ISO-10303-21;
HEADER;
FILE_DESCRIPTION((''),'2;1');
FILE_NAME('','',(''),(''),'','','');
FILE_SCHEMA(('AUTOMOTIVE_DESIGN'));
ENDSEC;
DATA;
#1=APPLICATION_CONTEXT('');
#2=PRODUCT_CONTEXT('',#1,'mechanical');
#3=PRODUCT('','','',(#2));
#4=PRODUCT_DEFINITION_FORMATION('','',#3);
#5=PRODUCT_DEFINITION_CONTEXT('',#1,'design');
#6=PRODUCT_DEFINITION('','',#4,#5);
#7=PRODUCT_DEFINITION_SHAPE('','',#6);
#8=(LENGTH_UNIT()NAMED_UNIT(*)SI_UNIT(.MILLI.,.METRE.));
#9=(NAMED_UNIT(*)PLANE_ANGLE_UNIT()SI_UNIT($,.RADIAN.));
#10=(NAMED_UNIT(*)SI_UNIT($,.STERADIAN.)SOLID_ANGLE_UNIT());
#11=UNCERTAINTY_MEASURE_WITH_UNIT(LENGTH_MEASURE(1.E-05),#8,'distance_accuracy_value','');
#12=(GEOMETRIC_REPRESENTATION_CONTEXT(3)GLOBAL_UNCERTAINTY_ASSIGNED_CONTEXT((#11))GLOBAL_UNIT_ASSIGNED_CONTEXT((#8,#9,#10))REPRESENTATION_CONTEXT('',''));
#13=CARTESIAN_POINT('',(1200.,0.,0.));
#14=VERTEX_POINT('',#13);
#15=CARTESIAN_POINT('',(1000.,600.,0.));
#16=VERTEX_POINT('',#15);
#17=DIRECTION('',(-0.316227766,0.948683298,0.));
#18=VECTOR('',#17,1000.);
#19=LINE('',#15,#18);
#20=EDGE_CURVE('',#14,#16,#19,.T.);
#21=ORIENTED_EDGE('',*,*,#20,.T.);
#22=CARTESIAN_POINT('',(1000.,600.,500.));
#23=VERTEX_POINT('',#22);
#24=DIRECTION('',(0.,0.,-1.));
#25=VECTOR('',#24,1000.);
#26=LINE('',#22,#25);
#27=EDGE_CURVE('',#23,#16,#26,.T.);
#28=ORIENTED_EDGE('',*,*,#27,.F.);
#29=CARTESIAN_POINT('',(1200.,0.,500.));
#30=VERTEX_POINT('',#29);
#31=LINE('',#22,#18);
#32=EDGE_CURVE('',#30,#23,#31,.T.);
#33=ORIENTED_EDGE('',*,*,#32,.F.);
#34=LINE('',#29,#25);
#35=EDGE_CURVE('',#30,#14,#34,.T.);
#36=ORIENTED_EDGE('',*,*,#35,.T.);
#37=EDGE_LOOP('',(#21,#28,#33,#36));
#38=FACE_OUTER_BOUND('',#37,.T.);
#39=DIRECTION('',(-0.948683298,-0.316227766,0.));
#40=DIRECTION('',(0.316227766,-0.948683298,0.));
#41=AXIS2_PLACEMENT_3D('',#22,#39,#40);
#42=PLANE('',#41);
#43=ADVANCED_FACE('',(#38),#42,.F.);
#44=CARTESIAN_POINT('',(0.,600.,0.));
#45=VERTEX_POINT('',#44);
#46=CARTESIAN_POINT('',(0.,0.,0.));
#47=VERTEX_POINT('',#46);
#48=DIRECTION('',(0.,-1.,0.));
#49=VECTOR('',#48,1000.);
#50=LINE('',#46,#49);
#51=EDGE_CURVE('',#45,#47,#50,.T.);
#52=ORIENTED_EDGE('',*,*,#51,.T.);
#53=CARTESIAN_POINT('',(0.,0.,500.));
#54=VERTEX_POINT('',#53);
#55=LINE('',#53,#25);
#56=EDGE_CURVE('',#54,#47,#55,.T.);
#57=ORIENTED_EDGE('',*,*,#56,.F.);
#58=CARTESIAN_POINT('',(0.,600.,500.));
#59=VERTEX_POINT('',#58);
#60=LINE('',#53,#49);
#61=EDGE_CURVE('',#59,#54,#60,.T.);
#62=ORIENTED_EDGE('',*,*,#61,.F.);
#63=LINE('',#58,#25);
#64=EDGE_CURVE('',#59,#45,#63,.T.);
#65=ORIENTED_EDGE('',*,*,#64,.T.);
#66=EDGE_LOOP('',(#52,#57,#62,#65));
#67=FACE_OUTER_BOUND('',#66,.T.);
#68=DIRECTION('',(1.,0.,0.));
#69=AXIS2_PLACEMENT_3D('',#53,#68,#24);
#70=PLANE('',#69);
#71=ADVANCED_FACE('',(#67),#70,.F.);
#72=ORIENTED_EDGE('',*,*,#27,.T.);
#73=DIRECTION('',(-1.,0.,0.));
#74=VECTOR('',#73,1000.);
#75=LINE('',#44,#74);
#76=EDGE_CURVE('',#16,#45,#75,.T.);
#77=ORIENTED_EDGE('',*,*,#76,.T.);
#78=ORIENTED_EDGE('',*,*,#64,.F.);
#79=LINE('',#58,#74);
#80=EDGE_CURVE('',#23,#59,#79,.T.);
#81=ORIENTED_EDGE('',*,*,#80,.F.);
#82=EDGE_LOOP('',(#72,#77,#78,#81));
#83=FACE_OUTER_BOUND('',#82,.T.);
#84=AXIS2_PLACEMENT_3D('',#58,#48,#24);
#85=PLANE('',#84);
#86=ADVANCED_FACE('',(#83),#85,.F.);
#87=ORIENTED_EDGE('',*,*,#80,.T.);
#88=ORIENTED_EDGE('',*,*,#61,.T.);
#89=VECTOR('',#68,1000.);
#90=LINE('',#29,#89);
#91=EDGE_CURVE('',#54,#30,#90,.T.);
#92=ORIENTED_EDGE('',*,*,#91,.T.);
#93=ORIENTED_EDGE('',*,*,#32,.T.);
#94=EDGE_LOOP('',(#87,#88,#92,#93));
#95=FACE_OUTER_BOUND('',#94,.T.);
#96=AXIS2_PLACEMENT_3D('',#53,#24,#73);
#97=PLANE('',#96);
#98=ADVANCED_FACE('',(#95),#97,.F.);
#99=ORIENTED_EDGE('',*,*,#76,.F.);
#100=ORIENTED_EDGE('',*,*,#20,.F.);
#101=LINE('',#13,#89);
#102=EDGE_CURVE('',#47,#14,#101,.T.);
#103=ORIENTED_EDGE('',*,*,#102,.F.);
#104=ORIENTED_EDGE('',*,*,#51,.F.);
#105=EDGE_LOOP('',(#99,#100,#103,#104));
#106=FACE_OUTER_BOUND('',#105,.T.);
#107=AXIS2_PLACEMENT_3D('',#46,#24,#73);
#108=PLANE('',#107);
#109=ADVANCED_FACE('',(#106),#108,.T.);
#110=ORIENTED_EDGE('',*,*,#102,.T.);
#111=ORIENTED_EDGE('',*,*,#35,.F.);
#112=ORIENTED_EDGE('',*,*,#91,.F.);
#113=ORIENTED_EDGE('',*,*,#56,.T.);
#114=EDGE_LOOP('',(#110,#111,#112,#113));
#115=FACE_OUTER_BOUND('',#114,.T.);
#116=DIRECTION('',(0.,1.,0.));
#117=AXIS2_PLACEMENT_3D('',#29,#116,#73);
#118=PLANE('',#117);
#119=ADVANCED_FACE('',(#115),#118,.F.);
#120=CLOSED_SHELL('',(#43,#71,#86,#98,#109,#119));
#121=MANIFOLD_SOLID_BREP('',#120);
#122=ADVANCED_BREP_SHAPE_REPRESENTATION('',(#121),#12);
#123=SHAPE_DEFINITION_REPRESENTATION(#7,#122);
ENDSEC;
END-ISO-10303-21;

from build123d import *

# Parameters (mm, degrees)
BOSS_EXTRUDE1_DEPTH = 500


with BuildPart() as part:
    # Sketch1 → Boss-Extrude1 (new body)
    with BuildSketch(Plane.XY):
        Polygon((0, 0), (0, 600), (1000, 600), (1200, 0), align=None)
    extrude(amount=BOSS_EXTRUDE1_DEPTH)


solid = part.part
